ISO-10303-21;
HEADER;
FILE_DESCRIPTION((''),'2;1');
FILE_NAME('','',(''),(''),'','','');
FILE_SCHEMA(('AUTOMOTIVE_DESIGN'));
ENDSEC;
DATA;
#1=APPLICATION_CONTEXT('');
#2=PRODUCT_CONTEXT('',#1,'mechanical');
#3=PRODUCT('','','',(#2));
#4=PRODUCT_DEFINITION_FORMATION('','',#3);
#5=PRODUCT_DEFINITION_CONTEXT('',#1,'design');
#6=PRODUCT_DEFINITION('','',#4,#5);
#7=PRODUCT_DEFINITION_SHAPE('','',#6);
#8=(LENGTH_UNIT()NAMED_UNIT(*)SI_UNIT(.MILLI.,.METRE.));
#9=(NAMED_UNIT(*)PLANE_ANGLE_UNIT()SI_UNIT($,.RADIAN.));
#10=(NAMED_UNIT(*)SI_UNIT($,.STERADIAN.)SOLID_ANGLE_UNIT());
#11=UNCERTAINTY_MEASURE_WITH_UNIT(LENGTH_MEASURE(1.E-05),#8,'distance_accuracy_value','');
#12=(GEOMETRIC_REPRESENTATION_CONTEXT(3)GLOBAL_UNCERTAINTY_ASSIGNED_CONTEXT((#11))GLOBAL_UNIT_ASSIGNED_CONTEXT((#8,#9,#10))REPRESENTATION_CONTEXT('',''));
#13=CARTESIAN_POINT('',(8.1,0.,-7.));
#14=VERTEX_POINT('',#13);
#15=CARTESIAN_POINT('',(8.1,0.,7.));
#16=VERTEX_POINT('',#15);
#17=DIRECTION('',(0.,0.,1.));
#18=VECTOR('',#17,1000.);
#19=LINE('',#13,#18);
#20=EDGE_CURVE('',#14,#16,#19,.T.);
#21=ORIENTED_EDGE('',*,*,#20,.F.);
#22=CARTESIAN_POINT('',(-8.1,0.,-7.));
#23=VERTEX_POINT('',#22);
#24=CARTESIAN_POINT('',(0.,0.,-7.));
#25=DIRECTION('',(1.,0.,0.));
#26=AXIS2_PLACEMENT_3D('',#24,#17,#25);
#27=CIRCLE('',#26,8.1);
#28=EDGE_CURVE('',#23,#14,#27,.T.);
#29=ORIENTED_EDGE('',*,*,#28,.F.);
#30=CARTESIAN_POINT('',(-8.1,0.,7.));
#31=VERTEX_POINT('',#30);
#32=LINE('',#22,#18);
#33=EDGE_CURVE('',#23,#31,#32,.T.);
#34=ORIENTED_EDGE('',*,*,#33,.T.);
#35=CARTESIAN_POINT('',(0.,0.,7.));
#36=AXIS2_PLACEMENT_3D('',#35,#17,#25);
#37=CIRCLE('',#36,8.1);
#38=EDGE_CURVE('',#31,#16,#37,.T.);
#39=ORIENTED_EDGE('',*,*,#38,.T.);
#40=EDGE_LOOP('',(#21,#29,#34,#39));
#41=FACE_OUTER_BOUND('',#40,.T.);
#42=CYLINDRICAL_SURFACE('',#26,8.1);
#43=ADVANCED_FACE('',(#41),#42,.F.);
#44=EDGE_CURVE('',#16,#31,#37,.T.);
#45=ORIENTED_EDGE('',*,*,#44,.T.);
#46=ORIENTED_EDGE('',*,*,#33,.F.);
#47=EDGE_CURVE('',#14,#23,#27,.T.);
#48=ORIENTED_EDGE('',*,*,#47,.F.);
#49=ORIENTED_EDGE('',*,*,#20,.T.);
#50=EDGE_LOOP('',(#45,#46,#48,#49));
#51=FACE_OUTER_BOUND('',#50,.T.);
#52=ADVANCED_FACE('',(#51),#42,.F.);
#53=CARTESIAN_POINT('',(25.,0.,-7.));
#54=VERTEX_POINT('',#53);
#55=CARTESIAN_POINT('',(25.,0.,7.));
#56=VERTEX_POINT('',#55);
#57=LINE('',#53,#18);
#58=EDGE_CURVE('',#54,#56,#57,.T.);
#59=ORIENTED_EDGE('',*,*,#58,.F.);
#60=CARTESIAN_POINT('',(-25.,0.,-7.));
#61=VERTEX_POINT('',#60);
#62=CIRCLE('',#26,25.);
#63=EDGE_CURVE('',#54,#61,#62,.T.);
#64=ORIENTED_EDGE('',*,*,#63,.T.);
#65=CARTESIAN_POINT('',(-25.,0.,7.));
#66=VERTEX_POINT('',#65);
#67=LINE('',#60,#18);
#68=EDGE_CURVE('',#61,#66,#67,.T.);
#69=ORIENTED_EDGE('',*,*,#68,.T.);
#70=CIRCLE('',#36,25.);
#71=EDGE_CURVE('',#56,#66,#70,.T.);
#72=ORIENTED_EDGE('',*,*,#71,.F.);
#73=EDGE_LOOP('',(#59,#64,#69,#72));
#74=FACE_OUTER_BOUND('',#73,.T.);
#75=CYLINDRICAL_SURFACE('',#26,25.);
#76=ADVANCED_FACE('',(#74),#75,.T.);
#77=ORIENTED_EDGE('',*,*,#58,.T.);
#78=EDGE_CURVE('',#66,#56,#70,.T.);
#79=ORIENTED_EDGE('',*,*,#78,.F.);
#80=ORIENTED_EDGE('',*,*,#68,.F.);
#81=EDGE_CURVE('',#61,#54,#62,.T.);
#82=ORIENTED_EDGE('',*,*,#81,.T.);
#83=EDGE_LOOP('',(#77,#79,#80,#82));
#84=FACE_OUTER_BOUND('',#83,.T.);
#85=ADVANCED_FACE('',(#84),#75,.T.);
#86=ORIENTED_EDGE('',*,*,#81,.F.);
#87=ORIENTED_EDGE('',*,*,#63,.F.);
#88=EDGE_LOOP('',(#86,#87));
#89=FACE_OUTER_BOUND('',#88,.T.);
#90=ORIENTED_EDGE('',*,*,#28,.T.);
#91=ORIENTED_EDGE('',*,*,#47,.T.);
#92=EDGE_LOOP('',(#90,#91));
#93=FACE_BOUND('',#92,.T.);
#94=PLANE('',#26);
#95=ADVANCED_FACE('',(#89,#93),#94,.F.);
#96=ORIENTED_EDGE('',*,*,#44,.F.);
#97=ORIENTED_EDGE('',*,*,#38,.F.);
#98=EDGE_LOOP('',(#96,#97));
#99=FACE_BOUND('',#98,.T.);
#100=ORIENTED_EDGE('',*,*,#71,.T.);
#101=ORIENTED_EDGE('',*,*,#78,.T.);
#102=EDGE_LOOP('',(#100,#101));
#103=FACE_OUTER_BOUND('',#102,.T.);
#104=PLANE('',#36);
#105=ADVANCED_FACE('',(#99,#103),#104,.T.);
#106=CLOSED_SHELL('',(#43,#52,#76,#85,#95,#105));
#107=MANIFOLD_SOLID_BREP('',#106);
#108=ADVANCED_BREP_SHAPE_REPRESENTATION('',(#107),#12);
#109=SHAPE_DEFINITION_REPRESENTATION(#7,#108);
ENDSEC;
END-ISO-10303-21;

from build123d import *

# Parameters (mm, degrees)
SKETCH_1_R      = 25
SKETCH_1_R_2    = 8.1
EXTRUDE_1_DEPTH = 7


with BuildPart() as part:
    # 草图1 → 凸台-拉伸1 (new, symmetric)
    with BuildSketch(Plane.XY):
        Circle(SKETCH_1_R)
        Circle(SKETCH_1_R_2, mode=Mode.SUBTRACT)
    extrude(amount=EXTRUDE_1_DEPTH, both=True)


solid = part.part
